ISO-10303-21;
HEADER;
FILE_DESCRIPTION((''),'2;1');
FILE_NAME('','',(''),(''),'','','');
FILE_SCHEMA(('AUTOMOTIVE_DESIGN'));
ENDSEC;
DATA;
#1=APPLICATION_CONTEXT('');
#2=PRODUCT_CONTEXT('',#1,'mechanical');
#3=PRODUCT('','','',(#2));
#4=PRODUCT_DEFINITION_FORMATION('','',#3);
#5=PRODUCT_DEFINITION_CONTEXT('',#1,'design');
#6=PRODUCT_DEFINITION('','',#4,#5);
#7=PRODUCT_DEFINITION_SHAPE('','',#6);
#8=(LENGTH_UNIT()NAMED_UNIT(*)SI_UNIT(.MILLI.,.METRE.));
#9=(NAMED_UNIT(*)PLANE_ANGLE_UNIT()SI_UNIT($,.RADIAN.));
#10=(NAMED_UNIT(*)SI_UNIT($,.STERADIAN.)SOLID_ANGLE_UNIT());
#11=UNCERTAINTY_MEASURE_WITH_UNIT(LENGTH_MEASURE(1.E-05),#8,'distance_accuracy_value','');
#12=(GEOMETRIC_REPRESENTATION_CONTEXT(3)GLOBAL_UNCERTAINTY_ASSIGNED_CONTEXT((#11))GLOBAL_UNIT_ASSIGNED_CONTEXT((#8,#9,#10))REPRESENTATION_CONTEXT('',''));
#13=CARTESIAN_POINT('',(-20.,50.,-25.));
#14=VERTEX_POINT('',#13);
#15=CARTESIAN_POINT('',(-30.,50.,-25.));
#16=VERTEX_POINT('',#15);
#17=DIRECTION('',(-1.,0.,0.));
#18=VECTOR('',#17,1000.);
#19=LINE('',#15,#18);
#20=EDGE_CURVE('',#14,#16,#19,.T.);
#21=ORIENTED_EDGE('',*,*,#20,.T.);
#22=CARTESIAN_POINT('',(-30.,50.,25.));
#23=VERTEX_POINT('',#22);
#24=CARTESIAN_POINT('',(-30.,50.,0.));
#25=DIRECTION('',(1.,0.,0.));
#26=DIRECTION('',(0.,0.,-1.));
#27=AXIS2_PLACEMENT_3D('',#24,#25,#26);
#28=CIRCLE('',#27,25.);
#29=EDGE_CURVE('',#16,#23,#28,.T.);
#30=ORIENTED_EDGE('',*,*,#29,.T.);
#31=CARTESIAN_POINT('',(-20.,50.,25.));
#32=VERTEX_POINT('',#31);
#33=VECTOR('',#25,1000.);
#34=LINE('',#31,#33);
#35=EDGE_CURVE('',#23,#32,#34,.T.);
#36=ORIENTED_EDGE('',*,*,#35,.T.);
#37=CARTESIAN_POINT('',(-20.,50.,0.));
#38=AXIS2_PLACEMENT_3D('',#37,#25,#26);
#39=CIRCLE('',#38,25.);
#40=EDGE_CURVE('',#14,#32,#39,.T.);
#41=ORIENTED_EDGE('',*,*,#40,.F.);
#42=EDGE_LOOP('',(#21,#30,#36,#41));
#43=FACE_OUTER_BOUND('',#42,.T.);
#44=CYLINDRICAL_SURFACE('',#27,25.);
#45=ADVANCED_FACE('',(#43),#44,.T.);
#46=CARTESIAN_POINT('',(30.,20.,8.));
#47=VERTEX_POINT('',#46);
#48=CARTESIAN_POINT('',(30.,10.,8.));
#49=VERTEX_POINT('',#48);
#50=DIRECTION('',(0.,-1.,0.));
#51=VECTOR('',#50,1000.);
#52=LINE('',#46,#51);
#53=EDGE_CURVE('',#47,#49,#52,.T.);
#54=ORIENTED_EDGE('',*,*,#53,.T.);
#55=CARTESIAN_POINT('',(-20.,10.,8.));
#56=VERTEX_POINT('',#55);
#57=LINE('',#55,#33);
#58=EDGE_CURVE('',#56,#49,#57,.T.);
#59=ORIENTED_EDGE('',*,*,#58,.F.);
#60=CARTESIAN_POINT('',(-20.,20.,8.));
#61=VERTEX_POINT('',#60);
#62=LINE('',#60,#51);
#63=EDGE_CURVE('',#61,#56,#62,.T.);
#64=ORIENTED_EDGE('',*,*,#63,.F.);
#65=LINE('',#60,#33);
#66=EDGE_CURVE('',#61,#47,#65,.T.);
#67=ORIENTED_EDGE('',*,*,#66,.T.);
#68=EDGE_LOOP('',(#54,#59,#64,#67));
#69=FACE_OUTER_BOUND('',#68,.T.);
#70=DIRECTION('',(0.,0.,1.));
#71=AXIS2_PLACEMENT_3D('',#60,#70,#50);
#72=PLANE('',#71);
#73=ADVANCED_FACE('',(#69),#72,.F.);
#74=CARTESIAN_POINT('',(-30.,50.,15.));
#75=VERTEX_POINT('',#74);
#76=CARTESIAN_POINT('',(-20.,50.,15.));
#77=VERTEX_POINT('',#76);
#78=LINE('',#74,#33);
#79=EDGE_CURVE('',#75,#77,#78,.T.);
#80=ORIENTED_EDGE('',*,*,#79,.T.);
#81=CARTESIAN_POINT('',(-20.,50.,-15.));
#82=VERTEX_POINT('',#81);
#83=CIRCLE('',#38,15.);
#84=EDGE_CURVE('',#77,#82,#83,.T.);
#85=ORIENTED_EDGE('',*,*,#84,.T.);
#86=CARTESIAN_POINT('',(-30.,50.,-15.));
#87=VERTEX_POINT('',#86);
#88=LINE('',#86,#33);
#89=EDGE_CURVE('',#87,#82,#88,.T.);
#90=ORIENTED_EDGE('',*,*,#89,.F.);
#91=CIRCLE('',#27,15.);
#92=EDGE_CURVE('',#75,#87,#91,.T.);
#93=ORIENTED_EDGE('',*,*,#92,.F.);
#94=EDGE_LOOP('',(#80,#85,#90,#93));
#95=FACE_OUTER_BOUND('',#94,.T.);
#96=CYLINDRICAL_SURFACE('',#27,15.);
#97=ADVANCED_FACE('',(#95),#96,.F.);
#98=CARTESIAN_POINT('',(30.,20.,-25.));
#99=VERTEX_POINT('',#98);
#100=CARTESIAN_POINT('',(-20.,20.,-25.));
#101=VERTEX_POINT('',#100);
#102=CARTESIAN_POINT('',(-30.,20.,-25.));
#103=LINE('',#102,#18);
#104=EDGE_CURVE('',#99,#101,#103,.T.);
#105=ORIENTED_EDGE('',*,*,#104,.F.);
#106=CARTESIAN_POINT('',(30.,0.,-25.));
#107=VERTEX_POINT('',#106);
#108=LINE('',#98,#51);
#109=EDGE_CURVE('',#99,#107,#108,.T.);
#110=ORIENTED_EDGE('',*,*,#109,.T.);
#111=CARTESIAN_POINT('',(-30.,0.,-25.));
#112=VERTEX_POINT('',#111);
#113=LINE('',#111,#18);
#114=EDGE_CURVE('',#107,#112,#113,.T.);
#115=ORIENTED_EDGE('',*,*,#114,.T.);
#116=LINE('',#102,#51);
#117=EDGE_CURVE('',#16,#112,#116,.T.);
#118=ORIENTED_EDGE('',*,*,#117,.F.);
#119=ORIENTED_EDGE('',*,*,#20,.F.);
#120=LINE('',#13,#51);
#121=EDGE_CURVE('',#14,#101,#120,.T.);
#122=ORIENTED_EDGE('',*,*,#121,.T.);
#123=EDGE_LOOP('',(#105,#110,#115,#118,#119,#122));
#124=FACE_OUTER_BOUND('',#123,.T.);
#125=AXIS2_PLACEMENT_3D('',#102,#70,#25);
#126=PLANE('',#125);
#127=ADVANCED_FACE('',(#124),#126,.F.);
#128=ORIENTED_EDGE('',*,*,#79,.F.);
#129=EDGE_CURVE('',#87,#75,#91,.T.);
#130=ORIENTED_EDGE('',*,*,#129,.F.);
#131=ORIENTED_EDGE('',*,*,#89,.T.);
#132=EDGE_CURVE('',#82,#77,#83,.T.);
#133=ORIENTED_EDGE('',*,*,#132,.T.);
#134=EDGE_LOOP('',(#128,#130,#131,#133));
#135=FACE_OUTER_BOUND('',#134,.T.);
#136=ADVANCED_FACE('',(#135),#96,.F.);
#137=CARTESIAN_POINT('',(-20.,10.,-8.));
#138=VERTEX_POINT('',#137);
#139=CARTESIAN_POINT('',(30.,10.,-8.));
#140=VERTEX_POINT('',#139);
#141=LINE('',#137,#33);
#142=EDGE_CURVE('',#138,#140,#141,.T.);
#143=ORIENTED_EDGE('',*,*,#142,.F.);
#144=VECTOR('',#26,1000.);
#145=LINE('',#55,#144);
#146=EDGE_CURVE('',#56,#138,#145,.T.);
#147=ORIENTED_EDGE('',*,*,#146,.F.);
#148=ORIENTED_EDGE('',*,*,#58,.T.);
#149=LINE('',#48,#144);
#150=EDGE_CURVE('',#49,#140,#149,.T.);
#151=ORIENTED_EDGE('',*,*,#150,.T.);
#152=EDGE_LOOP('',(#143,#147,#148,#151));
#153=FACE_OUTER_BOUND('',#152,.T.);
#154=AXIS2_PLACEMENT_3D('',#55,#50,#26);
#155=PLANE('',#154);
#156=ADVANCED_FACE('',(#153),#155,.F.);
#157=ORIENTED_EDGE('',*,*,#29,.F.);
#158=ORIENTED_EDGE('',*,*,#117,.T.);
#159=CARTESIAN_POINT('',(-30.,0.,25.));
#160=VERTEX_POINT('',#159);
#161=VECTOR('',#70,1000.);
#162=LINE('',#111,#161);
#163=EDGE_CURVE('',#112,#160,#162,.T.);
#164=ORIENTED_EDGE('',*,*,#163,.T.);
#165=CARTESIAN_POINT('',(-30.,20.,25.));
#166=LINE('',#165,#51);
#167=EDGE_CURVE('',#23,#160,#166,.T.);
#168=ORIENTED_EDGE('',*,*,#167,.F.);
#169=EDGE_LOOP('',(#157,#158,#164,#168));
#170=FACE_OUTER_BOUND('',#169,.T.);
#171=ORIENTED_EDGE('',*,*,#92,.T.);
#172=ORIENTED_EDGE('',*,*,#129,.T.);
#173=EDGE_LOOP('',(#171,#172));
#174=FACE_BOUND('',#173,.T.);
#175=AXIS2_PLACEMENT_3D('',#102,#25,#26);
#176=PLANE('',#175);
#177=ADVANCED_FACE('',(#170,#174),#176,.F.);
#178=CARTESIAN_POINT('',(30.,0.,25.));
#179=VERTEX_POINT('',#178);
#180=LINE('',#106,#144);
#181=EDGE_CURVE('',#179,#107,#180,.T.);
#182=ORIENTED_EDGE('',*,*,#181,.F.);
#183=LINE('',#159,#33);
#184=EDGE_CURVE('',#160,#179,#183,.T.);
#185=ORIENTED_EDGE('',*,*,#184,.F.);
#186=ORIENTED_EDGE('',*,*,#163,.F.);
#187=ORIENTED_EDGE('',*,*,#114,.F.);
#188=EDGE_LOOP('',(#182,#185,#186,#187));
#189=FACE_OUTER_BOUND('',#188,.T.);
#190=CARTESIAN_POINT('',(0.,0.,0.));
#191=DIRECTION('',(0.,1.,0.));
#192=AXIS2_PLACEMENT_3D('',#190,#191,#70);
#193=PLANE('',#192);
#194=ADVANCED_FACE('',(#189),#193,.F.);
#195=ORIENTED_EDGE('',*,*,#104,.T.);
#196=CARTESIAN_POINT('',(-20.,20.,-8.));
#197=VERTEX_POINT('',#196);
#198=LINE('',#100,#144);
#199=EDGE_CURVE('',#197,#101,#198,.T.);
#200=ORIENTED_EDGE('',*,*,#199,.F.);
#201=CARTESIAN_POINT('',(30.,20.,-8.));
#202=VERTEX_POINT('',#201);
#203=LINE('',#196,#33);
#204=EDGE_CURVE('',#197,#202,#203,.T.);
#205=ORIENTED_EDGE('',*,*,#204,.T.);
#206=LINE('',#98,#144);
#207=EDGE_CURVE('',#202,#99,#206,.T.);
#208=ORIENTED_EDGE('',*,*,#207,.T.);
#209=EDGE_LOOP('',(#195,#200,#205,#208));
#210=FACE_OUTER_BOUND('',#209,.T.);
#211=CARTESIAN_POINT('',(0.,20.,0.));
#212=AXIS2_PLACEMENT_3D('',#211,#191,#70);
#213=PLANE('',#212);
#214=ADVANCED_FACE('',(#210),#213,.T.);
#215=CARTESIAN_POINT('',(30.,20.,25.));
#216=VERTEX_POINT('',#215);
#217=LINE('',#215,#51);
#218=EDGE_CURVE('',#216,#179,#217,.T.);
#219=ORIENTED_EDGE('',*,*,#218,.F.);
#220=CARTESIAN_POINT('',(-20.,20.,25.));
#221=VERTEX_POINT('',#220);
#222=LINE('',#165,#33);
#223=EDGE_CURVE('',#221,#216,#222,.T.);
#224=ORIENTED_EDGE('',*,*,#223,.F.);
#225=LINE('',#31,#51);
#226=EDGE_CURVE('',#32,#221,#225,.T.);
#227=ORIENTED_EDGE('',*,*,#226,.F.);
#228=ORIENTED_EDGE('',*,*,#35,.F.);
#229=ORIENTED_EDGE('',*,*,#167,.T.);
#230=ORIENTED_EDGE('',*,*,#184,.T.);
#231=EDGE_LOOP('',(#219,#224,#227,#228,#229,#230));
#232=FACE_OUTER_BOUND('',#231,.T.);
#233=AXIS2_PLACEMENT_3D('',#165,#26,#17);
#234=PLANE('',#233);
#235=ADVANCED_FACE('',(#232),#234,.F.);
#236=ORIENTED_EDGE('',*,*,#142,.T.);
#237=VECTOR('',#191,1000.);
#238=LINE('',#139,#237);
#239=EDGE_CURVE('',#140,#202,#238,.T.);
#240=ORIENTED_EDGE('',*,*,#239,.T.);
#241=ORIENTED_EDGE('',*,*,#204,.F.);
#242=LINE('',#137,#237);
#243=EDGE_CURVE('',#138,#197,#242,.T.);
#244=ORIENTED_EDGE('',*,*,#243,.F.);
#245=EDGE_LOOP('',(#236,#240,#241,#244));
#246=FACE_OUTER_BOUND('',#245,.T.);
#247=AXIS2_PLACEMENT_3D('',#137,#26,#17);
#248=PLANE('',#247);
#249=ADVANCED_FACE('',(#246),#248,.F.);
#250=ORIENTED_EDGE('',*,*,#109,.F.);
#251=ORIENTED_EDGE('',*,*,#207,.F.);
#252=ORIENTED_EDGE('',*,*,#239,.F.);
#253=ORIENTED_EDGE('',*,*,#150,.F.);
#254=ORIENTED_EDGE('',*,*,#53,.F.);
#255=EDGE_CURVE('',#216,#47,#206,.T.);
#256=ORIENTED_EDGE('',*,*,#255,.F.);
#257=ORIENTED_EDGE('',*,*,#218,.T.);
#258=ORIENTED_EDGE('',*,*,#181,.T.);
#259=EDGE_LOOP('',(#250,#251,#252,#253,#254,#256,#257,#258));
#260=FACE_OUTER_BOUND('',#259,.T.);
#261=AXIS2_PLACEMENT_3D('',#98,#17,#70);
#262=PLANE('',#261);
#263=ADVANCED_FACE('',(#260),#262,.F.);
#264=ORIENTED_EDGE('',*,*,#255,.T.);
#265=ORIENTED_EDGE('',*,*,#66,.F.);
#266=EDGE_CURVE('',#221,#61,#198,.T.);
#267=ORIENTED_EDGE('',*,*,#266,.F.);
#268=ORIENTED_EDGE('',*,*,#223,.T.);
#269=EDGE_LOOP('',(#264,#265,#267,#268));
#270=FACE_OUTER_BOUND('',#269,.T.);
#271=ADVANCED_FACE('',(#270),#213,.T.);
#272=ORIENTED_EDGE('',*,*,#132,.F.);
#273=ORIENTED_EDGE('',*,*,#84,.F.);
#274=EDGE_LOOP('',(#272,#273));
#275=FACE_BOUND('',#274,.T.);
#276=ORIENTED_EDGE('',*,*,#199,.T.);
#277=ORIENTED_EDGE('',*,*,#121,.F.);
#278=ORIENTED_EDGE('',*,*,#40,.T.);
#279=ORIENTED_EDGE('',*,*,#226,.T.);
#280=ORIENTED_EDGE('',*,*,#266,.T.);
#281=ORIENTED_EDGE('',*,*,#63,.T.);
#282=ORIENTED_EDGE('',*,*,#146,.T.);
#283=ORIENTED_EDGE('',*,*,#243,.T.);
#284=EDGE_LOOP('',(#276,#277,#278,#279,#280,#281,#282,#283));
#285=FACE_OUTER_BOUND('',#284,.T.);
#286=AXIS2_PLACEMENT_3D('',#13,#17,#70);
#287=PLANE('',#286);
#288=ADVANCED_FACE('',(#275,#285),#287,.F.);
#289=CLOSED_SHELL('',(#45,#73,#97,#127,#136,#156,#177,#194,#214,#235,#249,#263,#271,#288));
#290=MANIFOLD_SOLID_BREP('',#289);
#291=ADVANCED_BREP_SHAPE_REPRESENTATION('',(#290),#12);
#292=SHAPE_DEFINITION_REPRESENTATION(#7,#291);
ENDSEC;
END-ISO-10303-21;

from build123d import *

# Parameters (mm, degrees)
BASE_BLOCK_SKETCH_W  = 60
BASE_BLOCK_SKETCH_H  = 50
BASE_BLOCK_DEPTH     = 20
UPRIGHT_SKETCH_W     = 10
UPRIGHT_SKETCH_H     = 50
UPRIGHT_DEPTH        = 30
ROUNDED_TOP_SKETCH_R = 25
ROUNDED_TOP_DEPTH    = 10
PIVOT_HOLE_SKETCH_R  = 15
PIVOT_HOLE_DEPTH     = 10
BASE_SLOT_SKETCH_W   = 16
BASE_SLOT_SKETCH_H   = 10
BASE_SLOT_DEPTH      = 50


with BuildPart() as part:
    # Base Block Sketch → Base Block (new body)
    with BuildSketch(Plane(origin=(0, 0, 0), x_dir=(1, 0, 0), z_dir=(0, 1, 0))):
        Rectangle(BASE_BLOCK_SKETCH_W, BASE_BLOCK_SKETCH_H)
    extrude(amount=BASE_BLOCK_DEPTH)

    # Upright Sketch → Upright (add)
    with BuildSketch(Plane(origin=(0, 20, 0), x_dir=(1, 0, 0), z_dir=(0, 1, 0))):
        with Locations((-25, 0)):
            Rectangle(UPRIGHT_SKETCH_W, UPRIGHT_SKETCH_H)
    extrude(amount=UPRIGHT_DEPTH)

    # Rounded Top Sketch → Rounded Top (add)
    with BuildSketch(Plane(origin=(-20, 0, 0), x_dir=(0, 0, -1), z_dir=(1, 0, 0))):
        with Locations((0, 50)):
            Circle(ROUNDED_TOP_SKETCH_R)
    extrude(amount=-ROUNDED_TOP_DEPTH)

    # Pivot Hole Sketch → Pivot Hole (cut)
    with BuildSketch(Plane(origin=(-20, 0, 0), x_dir=(0, 0, -1), z_dir=(1, 0, 0))):
        with Locations((0, 50)):
            Circle(PIVOT_HOLE_SKETCH_R)
    extrude(amount=-PIVOT_HOLE_DEPTH, mode=Mode.SUBTRACT)

    # Base Slot Sketch → Base Slot (cut)
    with BuildSketch(Plane(origin=(30, 0, 0), x_dir=(0, 0, -1), z_dir=(1, 0, 0))):
        with Locations((0, 15)):
            Rectangle(BASE_SLOT_SKETCH_W, BASE_SLOT_SKETCH_H)
    extrude(amount=-BASE_SLOT_DEPTH, mode=Mode.SUBTRACT)


solid = part.part
